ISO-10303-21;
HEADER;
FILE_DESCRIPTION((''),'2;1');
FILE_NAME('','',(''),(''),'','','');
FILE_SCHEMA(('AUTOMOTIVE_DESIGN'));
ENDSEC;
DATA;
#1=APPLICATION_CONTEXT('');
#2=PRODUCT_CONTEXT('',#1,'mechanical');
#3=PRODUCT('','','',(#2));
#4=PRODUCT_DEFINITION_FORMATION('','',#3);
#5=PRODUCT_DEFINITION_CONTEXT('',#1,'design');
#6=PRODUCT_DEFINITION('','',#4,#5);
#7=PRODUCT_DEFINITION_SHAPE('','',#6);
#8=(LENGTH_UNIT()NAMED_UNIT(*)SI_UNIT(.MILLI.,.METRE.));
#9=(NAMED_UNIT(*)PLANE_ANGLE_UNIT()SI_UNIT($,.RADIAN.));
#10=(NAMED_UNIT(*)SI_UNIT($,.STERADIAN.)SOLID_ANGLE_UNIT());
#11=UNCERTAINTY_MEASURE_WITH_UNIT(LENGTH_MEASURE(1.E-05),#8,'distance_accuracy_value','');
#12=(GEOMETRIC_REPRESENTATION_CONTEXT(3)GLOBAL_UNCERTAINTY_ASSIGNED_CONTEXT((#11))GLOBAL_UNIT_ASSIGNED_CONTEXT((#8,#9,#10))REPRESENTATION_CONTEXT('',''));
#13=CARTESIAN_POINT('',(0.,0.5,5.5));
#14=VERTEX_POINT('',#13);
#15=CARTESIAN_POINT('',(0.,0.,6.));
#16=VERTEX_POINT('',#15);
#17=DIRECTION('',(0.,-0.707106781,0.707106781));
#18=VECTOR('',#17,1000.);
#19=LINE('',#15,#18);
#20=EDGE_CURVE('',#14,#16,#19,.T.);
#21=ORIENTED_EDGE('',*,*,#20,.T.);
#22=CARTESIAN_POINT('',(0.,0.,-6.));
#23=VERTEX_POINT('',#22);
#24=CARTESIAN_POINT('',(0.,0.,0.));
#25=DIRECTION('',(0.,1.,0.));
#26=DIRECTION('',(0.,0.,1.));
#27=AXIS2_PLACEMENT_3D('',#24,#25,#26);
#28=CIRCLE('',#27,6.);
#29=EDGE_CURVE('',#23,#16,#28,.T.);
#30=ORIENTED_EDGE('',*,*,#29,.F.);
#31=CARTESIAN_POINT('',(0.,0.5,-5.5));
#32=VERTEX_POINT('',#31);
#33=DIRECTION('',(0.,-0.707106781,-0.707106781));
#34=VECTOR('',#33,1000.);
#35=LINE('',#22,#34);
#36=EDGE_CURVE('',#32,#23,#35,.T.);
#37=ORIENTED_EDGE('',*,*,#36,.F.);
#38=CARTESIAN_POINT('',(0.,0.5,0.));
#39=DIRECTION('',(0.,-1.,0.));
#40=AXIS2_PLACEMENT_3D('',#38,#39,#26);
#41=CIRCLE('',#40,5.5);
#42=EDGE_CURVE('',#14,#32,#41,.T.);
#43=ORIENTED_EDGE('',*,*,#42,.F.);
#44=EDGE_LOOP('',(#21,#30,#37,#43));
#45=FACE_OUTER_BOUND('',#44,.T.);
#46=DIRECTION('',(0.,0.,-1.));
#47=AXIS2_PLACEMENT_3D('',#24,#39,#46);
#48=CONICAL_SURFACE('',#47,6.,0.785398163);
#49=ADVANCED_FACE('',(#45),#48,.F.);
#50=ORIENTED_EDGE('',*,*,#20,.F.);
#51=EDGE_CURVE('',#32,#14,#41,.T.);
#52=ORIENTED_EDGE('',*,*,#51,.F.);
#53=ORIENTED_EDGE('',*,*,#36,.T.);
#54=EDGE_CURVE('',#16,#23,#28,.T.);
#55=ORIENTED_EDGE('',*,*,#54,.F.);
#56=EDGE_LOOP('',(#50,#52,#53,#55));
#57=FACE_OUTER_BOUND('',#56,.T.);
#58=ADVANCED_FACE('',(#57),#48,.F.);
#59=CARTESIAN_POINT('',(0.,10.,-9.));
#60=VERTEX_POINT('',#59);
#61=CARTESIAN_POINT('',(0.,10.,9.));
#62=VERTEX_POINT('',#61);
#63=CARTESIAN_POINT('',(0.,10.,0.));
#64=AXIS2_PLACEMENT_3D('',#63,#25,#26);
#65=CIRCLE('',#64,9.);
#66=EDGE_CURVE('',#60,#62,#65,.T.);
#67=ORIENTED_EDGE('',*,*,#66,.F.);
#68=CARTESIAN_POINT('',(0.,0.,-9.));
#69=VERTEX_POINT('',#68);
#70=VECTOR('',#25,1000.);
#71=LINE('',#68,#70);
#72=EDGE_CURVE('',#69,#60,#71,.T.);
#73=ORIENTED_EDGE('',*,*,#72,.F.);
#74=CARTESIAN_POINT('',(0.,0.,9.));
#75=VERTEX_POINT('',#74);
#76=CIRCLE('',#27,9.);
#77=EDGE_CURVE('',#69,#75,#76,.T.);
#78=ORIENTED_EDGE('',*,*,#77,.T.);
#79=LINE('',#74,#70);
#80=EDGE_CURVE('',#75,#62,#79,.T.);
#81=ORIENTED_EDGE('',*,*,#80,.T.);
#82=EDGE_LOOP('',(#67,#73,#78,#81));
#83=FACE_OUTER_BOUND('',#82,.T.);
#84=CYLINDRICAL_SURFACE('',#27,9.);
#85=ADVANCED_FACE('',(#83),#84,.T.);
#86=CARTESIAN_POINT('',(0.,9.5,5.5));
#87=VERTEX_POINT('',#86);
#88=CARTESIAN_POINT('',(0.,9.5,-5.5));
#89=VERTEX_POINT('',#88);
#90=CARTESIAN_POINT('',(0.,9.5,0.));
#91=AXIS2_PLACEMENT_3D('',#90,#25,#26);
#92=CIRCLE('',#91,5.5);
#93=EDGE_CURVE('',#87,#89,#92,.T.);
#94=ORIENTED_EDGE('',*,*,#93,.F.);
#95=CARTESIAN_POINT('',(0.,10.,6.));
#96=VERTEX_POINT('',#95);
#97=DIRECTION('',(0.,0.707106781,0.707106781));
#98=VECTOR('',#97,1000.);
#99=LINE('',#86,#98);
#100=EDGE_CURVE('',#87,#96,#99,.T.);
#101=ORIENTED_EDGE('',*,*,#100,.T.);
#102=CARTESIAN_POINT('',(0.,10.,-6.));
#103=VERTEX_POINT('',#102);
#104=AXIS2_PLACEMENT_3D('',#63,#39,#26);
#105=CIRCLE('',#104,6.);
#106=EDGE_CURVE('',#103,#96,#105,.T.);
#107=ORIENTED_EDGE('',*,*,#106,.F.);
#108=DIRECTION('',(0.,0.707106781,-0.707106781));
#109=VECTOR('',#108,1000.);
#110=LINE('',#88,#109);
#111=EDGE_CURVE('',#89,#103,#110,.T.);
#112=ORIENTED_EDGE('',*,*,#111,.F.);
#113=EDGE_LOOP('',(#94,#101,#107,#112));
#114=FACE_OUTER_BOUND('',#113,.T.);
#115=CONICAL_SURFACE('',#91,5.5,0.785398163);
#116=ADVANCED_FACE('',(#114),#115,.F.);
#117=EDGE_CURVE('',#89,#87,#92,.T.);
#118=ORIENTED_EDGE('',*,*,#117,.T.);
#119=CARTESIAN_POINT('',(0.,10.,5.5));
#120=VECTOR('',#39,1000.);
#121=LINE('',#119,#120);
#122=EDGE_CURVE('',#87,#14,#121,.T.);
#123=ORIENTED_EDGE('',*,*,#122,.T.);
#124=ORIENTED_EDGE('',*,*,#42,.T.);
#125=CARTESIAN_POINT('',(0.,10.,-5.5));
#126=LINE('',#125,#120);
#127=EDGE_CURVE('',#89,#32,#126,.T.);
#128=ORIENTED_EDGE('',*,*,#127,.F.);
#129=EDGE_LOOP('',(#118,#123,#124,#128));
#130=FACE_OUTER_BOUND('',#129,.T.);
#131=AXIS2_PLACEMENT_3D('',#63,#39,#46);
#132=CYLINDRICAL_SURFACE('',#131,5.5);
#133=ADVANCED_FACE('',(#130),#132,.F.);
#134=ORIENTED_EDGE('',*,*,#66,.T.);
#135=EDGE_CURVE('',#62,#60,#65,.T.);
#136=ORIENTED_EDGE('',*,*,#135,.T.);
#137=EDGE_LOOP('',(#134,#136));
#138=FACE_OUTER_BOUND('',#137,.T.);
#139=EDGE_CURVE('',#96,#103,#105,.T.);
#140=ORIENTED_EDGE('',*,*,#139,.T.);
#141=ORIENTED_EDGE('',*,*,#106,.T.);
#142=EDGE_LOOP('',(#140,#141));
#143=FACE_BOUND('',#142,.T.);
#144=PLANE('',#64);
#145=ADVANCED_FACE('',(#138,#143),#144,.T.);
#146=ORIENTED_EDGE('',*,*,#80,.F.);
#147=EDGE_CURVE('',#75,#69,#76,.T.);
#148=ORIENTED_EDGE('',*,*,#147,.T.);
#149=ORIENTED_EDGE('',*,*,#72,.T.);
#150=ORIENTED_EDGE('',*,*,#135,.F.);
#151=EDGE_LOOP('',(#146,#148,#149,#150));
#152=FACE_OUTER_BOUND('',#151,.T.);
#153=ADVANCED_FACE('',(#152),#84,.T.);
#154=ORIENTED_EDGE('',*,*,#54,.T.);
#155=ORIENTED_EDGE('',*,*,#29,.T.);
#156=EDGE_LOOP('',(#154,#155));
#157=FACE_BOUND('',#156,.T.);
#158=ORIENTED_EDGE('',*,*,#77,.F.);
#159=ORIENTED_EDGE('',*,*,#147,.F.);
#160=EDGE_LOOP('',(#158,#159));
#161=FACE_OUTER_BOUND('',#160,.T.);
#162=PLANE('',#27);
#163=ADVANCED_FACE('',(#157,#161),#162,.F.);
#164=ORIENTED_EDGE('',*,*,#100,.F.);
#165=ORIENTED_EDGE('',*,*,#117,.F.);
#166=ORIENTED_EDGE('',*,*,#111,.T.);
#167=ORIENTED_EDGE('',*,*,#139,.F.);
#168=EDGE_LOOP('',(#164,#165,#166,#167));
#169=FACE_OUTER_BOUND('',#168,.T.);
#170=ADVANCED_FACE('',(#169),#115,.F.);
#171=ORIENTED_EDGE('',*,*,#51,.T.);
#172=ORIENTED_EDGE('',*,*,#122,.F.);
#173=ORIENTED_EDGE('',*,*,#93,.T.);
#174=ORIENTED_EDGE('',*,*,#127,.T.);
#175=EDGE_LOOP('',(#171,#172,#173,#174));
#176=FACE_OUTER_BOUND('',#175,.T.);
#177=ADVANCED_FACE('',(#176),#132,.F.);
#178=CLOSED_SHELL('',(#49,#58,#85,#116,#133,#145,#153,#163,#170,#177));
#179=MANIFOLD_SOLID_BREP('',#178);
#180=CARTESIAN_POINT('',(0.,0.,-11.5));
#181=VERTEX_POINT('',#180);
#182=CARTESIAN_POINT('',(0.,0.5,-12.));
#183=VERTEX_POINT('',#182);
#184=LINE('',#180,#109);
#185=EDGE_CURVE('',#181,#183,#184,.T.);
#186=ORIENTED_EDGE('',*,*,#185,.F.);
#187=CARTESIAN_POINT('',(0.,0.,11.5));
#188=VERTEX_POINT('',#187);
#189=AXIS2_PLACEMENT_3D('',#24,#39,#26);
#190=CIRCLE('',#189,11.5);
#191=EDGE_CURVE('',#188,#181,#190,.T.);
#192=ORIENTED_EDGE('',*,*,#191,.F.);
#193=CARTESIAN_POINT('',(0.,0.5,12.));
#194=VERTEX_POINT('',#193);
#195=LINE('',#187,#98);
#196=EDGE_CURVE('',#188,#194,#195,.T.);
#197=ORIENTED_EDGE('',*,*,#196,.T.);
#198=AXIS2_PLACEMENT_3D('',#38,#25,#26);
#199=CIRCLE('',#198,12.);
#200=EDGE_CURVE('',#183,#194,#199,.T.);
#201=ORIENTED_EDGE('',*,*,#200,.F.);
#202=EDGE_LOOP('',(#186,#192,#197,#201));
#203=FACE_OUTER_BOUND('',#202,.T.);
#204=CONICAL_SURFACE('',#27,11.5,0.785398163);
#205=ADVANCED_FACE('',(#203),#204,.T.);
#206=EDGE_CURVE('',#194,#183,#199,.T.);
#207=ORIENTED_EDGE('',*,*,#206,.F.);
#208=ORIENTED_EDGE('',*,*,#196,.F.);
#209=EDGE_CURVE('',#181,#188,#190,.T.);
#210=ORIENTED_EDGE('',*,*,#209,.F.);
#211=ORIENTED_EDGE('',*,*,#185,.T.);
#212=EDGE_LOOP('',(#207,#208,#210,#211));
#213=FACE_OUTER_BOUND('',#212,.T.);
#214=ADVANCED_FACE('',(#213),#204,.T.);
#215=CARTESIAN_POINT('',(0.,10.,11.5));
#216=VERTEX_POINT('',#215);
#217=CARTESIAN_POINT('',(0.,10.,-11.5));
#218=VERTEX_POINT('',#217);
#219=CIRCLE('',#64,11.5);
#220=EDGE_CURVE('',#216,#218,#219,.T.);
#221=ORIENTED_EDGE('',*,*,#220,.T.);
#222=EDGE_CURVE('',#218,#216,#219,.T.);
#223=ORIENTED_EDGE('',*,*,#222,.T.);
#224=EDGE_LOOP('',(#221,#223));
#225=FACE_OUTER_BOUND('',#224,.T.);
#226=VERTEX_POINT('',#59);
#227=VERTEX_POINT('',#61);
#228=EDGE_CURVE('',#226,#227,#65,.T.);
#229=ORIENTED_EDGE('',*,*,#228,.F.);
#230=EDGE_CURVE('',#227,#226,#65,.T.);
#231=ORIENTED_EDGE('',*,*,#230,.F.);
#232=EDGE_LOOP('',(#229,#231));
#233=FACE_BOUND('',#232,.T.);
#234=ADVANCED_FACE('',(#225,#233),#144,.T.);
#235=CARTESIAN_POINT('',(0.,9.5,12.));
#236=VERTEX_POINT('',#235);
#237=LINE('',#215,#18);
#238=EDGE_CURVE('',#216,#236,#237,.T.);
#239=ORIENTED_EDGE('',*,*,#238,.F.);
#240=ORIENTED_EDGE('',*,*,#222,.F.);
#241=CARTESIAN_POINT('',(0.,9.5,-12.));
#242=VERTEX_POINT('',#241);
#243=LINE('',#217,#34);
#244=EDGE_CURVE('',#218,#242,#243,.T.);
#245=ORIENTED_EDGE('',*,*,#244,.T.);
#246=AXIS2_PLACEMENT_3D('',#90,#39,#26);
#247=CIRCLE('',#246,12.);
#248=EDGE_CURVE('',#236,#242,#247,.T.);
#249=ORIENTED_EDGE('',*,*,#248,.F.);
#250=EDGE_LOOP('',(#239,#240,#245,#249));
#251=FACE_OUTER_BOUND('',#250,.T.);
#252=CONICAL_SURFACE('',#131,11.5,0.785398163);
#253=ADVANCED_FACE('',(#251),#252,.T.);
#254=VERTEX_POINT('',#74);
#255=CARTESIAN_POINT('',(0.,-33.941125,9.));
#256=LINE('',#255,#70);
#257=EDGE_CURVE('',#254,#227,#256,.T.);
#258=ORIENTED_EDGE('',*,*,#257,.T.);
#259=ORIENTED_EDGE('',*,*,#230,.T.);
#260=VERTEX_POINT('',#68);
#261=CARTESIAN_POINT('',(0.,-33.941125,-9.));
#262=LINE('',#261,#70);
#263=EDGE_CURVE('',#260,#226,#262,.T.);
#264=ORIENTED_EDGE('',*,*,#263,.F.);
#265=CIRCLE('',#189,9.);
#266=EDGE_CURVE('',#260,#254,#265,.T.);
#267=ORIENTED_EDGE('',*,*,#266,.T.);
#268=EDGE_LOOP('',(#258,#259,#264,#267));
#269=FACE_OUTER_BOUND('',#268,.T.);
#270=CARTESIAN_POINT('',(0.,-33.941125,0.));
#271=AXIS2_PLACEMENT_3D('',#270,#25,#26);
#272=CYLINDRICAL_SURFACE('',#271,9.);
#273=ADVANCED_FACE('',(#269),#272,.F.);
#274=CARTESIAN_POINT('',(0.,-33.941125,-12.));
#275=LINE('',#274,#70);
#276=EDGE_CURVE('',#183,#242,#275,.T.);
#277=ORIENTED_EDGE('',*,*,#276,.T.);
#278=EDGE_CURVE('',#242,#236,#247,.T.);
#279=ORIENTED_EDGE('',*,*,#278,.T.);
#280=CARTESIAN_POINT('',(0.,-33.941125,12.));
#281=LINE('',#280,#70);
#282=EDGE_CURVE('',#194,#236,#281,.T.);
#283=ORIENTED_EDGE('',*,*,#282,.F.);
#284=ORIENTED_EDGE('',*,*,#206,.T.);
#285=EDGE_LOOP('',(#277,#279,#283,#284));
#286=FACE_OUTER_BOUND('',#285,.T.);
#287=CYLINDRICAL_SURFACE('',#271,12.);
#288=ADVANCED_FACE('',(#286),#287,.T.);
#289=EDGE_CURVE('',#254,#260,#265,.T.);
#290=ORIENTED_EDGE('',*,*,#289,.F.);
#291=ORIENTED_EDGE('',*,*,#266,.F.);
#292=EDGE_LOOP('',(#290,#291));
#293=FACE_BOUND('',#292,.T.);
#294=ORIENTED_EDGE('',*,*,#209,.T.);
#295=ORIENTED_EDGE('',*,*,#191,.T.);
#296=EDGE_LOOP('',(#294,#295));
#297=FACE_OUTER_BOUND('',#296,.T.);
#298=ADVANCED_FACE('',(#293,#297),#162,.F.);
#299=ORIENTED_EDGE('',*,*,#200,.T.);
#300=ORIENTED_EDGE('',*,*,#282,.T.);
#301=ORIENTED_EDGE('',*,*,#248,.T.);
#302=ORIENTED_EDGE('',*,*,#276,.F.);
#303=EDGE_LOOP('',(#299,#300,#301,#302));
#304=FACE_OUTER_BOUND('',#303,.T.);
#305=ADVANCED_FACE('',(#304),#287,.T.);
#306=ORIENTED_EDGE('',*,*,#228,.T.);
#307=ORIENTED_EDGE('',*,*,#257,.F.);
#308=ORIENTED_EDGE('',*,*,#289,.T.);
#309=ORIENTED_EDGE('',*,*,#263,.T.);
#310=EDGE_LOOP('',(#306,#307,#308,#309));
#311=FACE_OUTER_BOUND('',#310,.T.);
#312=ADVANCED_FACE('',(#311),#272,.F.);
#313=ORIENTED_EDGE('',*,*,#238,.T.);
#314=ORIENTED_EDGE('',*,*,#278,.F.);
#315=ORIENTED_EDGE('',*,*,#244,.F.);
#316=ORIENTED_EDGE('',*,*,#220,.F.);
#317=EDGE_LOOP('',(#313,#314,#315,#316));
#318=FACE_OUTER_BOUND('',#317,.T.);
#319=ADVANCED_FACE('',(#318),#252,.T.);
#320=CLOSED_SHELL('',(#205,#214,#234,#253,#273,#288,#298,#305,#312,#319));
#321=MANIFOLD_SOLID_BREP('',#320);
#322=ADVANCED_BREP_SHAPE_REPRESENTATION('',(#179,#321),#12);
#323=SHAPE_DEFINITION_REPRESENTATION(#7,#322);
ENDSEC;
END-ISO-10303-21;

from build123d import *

# Parameters (mm, degrees)
SKETCH1_R           = 15
SKETCH1_R_2         = 5.5
BOSS_EXTRUDE1_DEPTH = 10
CHAMFER1_SIZE       = 0.5
CUT_EXTRUDE1_START  = -10
SKETCH2_R           = 15
SKETCH2_R_2         = 9
CUT_EXTRUDE1_DEPTH  = 10
SKETCH3_R           = 12
SKETCH3_R_2         = 9
BOSS_EXTRUDE2_DEPTH = 10
CHAMFER2_SIZE       = 0.5
CHAMFER3_SIZE       = 0.5


with BuildPart() as part:
    # Sketch1 → Boss-Extrude1 (new body)
    with BuildSketch(Plane(origin=(0, 0, 0), x_dir=(1, 0, 0), z_dir=(0, 1, 0))):
        with Locations(Location((0, 0, 0), (0, 0, 270))):
            Circle(SKETCH1_R)
        with Locations(Location((0, 0, 0), (0, 0, 270))):
            Circle(SKETCH1_R_2, mode=Mode.SUBTRACT)
    extrude(amount=BOSS_EXTRUDE1_DEPTH)

    # Chamfer1
    chamfer1_edges = [part.edges().sort_by_distance(p)[0] for p in [
        (0, 0, -15),
        (0, 10, -15),
    ]]
    chamfer(chamfer1_edges, length=CHAMFER1_SIZE)

    # Sketch2 → Cut-Extrude1 (cut)
    with BuildSketch(Plane(origin=(0, 10, 0), x_dir=(1, 0, 0), z_dir=(0, 1, 0)).offset(CUT_EXTRUDE1_START)):
        Circle(SKETCH2_R)
        with Locations(Location((0, 0, 0), (0, 0, 270))):
            Circle(SKETCH2_R_2, mode=Mode.SUBTRACT)
    extrude(amount=CUT_EXTRUDE1_DEPTH, mode=Mode.SUBTRACT)

    # Chamfer3
    chamfer3_edges = [part.edges().sort_by_distance(p)[0] for p in [
        (0, 0, -5.5),
        (0, 10, -5.5),
    ]]
    chamfer(chamfer3_edges, length=CHAMFER3_SIZE)


with BuildPart() as body_2:
    # Sketch3 → Boss-Extrude2 (new body)
    with BuildSketch(Plane(origin=(0, 10, 0), x_dir=(1, 0, 0), z_dir=(0, 1, 0))):
        with Locations(Location((0, 0, 0), (0, 0, 270))):
            Circle(SKETCH3_R)
        with Locations(Location((0, 0, 0), (0, 0, 270))):
            Circle(SKETCH3_R_2, mode=Mode.SUBTRACT)
    extrude(amount=-BOSS_EXTRUDE2_DEPTH)

    # Chamfer2
    chamfer2_edges = [body_2.edges().sort_by_distance(p)[0] for p in [
        (0, 10, -12),
        (0, 0, -12),
    ]]
    chamfer(chamfer2_edges, length=CHAMFER2_SIZE)


solid = Compound([part.part, body_2.part])
